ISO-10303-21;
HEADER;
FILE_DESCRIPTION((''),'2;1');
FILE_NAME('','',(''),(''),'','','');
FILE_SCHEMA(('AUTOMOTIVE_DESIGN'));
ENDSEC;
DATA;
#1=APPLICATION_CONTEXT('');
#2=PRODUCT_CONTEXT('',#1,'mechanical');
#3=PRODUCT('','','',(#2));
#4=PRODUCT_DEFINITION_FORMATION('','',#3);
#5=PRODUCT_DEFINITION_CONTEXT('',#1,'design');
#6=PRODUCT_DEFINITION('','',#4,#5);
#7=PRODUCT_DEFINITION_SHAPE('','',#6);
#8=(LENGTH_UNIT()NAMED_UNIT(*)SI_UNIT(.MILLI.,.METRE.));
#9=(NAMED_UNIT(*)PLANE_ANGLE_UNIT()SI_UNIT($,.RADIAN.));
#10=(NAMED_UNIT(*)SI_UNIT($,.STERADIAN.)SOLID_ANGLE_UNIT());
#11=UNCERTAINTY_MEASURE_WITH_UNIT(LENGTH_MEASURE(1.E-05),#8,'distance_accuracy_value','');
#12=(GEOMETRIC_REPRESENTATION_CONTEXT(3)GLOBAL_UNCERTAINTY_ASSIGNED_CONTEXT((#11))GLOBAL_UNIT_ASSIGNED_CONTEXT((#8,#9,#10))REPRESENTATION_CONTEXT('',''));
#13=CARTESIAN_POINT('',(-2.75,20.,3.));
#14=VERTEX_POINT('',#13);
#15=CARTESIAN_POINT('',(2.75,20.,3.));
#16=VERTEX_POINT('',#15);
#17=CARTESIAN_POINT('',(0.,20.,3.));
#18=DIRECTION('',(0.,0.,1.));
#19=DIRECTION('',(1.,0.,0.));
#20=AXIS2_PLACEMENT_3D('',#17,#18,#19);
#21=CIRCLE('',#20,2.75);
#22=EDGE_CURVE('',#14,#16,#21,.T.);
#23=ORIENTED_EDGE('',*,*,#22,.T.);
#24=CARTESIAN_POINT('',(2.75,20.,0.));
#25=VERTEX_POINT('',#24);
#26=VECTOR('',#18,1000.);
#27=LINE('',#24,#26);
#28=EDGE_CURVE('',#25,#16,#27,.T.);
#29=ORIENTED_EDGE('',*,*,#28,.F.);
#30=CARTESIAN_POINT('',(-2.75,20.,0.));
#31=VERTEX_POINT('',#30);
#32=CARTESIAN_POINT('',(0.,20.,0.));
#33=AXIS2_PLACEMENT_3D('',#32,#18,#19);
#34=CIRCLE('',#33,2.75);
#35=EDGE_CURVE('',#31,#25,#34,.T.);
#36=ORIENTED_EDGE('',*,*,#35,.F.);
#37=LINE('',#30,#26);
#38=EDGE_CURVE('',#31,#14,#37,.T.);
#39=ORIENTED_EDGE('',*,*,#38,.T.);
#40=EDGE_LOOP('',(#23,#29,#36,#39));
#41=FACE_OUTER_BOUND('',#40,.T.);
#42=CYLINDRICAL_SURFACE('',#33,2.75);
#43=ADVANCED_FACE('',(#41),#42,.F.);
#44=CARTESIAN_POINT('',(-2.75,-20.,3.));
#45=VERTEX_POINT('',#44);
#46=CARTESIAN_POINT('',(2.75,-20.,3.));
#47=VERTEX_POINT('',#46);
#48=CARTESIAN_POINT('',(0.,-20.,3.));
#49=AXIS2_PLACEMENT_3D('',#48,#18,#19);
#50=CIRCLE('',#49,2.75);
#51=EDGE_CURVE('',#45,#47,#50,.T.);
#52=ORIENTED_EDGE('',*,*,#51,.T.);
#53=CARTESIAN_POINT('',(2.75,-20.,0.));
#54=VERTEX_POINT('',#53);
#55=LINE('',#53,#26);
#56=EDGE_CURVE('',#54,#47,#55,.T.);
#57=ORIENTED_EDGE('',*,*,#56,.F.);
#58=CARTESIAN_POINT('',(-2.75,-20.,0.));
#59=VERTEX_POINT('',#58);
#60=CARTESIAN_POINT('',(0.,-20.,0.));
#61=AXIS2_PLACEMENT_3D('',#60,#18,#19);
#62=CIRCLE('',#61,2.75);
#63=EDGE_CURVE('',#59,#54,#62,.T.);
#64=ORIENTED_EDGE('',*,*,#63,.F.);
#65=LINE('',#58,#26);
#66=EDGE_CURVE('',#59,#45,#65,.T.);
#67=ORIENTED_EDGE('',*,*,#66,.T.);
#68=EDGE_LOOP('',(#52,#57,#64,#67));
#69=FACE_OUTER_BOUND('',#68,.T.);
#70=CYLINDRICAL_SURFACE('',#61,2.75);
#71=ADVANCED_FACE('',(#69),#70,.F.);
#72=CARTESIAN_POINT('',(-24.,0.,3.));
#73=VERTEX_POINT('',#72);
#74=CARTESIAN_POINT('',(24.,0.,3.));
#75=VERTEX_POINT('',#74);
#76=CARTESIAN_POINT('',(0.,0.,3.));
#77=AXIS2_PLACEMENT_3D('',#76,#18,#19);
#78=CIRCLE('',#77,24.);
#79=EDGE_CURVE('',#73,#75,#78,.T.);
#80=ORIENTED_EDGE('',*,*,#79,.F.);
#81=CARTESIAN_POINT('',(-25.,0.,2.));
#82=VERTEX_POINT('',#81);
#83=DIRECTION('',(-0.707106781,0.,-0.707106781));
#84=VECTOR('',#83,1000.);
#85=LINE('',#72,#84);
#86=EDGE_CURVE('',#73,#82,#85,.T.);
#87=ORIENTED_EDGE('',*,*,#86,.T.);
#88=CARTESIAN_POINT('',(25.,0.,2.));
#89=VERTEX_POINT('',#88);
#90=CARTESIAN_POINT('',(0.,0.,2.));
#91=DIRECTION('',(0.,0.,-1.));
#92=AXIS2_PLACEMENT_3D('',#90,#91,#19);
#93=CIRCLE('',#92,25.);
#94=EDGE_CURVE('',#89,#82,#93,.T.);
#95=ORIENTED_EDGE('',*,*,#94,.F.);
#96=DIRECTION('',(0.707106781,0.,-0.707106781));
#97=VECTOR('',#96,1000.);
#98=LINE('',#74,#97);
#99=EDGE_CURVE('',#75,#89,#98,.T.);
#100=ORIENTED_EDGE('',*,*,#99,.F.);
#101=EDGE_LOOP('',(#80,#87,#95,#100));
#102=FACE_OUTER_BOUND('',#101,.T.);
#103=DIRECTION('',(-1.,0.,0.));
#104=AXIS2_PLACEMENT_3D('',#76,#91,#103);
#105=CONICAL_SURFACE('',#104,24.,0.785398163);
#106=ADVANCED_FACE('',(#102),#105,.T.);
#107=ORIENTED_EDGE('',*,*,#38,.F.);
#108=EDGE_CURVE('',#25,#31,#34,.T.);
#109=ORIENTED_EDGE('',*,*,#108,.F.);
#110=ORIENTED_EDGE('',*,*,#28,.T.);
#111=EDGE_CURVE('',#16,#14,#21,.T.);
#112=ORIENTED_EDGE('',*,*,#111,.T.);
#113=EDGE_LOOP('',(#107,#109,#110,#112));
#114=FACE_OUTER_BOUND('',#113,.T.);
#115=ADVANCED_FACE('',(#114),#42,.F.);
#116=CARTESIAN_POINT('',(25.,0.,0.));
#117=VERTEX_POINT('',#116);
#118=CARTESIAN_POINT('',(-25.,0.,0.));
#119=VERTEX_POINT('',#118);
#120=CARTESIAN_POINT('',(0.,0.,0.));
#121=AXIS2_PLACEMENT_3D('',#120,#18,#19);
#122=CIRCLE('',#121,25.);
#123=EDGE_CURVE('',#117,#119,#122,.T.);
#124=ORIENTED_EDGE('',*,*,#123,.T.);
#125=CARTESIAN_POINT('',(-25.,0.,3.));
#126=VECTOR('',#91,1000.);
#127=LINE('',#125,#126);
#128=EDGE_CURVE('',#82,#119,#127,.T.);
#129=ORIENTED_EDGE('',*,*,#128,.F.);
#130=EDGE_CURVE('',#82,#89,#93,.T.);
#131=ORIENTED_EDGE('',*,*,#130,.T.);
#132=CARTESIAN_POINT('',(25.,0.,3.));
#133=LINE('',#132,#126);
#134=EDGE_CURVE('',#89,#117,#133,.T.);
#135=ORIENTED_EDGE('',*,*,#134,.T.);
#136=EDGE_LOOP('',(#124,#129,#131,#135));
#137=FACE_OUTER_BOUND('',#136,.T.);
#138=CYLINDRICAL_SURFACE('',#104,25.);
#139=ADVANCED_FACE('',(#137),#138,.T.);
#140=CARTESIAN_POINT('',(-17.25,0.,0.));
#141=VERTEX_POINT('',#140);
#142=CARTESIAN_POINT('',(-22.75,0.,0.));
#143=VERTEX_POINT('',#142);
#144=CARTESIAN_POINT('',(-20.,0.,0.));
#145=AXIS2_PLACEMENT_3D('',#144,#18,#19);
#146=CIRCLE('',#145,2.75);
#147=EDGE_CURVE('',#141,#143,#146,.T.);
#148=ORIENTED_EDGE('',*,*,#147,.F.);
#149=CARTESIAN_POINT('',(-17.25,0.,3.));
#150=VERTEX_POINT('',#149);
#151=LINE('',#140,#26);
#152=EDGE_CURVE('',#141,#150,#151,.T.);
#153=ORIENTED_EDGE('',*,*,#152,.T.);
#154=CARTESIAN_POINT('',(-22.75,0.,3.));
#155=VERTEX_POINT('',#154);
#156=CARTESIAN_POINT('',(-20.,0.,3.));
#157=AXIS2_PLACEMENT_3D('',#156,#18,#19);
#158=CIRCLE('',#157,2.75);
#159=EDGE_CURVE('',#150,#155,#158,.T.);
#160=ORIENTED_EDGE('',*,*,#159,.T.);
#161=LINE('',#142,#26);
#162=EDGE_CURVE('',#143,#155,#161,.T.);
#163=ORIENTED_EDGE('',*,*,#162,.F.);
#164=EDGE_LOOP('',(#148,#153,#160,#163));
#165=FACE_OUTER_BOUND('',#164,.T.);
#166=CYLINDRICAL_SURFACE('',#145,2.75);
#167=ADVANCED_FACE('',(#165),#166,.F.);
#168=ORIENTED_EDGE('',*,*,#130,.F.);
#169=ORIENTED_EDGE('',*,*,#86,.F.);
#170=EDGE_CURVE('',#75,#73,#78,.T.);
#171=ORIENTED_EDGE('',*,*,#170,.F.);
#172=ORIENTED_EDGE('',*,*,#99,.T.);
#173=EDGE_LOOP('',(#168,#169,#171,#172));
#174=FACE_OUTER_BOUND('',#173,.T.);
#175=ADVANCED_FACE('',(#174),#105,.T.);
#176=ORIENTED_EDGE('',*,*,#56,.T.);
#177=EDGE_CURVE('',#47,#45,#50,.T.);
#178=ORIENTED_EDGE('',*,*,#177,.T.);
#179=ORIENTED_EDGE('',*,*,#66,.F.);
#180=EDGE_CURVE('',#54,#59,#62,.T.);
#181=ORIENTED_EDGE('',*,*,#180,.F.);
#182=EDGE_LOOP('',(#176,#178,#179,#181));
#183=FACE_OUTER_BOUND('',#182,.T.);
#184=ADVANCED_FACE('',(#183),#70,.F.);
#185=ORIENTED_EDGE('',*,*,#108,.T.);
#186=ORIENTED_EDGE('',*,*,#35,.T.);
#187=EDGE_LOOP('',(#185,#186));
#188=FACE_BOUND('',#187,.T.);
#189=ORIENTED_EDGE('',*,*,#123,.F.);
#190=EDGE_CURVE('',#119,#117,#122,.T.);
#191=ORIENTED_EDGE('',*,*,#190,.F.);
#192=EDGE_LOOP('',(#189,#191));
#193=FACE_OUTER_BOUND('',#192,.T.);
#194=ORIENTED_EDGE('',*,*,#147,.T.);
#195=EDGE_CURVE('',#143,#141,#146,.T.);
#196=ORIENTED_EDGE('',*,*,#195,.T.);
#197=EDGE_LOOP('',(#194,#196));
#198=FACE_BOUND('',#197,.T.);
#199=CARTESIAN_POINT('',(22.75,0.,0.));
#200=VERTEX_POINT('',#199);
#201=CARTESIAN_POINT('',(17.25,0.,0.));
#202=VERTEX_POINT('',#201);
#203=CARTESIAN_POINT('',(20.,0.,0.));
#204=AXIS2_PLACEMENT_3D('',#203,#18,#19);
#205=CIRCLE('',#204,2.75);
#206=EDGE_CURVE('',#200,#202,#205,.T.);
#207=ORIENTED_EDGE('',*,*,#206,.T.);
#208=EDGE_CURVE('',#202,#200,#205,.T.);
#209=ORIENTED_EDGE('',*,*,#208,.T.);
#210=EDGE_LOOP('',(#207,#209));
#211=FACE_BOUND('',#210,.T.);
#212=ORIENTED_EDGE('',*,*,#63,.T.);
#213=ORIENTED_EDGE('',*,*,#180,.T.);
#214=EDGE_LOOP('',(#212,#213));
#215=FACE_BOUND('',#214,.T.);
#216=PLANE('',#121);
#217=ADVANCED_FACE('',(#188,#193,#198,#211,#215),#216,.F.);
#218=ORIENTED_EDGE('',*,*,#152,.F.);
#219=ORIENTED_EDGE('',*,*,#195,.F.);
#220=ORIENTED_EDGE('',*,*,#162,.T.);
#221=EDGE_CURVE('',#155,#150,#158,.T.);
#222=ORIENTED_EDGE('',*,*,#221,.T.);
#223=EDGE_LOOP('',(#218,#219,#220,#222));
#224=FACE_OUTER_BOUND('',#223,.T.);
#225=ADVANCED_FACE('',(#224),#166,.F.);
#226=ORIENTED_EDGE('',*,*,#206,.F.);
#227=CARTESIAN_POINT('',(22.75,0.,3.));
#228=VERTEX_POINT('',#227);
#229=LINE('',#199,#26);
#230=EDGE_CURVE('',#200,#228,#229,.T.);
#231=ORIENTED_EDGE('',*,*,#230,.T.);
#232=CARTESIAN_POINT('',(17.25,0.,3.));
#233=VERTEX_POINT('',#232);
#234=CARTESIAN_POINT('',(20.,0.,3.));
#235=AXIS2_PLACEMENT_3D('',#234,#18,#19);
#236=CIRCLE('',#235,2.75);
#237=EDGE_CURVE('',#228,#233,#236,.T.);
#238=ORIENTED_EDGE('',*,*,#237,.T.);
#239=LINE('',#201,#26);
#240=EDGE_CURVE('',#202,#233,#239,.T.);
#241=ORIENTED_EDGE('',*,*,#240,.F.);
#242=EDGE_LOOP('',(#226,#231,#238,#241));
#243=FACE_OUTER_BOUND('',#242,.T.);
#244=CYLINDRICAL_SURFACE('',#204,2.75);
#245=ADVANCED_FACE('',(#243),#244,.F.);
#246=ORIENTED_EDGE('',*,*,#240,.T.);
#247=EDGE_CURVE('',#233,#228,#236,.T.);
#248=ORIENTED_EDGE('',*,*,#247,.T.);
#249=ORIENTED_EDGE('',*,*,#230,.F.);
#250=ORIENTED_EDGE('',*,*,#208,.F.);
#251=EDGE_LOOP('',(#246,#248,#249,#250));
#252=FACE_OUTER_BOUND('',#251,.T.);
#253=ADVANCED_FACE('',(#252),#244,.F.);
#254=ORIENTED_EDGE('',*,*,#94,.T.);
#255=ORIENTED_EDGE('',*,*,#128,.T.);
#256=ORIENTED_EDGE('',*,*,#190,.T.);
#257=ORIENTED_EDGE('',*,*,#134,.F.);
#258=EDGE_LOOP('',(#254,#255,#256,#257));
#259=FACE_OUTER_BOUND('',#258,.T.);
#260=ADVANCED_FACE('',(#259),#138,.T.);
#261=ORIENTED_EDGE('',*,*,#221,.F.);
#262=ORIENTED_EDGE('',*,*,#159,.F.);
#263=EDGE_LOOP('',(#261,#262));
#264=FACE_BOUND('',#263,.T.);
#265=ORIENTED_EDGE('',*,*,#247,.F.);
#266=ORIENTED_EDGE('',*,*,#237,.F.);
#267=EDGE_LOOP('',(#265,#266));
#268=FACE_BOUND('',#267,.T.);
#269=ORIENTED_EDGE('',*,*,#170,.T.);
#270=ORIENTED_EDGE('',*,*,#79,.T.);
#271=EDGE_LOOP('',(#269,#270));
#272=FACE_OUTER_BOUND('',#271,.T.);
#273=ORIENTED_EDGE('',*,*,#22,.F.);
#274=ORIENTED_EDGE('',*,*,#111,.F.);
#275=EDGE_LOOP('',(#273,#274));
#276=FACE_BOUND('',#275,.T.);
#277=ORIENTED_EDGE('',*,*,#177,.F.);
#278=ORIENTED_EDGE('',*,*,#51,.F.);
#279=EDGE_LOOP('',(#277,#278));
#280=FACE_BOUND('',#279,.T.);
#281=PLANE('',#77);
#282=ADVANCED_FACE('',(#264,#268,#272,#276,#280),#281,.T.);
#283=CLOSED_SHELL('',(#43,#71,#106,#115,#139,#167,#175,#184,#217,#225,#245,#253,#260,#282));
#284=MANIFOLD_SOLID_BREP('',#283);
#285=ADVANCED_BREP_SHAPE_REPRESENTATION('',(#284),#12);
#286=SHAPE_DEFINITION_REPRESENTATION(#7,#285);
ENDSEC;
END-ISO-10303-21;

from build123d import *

# Parameters (mm, degrees)
SKETCH1_R           = 25
BOSS_EXTRUDE1_DEPTH = 3
CHAMFER1_SIZE       = 1
SKETCH2_R           = 2.75
CUT_EXTRUDE1_DEPTH  = 3


with BuildPart() as part:
    # Sketch1 → Boss-Extrude1 (new body)
    with BuildSketch(Plane.XY):
        Circle(SKETCH1_R)
    extrude(amount=BOSS_EXTRUDE1_DEPTH)

    # Chamfer1
    chamfer1_edges = [part.edges().sort_by_distance(p)[0] for p in [
        (-25, 0, 3),
    ]]
    chamfer(chamfer1_edges, length=CHAMFER1_SIZE)

    # Sketch2 → Cut-Extrude1 (cut)
    with BuildSketch(Plane.XY.offset(3)):
        with Locations((20, 0)):
            Circle(SKETCH2_R)
        with Locations((0, -20)):
            Circle(SKETCH2_R)
        with Locations((-20, 0)):
            Circle(SKETCH2_R)
        with Locations((0, 20)):
            Circle(SKETCH2_R)
    extrude(amount=-CUT_EXTRUDE1_DEPTH, mode=Mode.SUBTRACT)


solid = part.part
